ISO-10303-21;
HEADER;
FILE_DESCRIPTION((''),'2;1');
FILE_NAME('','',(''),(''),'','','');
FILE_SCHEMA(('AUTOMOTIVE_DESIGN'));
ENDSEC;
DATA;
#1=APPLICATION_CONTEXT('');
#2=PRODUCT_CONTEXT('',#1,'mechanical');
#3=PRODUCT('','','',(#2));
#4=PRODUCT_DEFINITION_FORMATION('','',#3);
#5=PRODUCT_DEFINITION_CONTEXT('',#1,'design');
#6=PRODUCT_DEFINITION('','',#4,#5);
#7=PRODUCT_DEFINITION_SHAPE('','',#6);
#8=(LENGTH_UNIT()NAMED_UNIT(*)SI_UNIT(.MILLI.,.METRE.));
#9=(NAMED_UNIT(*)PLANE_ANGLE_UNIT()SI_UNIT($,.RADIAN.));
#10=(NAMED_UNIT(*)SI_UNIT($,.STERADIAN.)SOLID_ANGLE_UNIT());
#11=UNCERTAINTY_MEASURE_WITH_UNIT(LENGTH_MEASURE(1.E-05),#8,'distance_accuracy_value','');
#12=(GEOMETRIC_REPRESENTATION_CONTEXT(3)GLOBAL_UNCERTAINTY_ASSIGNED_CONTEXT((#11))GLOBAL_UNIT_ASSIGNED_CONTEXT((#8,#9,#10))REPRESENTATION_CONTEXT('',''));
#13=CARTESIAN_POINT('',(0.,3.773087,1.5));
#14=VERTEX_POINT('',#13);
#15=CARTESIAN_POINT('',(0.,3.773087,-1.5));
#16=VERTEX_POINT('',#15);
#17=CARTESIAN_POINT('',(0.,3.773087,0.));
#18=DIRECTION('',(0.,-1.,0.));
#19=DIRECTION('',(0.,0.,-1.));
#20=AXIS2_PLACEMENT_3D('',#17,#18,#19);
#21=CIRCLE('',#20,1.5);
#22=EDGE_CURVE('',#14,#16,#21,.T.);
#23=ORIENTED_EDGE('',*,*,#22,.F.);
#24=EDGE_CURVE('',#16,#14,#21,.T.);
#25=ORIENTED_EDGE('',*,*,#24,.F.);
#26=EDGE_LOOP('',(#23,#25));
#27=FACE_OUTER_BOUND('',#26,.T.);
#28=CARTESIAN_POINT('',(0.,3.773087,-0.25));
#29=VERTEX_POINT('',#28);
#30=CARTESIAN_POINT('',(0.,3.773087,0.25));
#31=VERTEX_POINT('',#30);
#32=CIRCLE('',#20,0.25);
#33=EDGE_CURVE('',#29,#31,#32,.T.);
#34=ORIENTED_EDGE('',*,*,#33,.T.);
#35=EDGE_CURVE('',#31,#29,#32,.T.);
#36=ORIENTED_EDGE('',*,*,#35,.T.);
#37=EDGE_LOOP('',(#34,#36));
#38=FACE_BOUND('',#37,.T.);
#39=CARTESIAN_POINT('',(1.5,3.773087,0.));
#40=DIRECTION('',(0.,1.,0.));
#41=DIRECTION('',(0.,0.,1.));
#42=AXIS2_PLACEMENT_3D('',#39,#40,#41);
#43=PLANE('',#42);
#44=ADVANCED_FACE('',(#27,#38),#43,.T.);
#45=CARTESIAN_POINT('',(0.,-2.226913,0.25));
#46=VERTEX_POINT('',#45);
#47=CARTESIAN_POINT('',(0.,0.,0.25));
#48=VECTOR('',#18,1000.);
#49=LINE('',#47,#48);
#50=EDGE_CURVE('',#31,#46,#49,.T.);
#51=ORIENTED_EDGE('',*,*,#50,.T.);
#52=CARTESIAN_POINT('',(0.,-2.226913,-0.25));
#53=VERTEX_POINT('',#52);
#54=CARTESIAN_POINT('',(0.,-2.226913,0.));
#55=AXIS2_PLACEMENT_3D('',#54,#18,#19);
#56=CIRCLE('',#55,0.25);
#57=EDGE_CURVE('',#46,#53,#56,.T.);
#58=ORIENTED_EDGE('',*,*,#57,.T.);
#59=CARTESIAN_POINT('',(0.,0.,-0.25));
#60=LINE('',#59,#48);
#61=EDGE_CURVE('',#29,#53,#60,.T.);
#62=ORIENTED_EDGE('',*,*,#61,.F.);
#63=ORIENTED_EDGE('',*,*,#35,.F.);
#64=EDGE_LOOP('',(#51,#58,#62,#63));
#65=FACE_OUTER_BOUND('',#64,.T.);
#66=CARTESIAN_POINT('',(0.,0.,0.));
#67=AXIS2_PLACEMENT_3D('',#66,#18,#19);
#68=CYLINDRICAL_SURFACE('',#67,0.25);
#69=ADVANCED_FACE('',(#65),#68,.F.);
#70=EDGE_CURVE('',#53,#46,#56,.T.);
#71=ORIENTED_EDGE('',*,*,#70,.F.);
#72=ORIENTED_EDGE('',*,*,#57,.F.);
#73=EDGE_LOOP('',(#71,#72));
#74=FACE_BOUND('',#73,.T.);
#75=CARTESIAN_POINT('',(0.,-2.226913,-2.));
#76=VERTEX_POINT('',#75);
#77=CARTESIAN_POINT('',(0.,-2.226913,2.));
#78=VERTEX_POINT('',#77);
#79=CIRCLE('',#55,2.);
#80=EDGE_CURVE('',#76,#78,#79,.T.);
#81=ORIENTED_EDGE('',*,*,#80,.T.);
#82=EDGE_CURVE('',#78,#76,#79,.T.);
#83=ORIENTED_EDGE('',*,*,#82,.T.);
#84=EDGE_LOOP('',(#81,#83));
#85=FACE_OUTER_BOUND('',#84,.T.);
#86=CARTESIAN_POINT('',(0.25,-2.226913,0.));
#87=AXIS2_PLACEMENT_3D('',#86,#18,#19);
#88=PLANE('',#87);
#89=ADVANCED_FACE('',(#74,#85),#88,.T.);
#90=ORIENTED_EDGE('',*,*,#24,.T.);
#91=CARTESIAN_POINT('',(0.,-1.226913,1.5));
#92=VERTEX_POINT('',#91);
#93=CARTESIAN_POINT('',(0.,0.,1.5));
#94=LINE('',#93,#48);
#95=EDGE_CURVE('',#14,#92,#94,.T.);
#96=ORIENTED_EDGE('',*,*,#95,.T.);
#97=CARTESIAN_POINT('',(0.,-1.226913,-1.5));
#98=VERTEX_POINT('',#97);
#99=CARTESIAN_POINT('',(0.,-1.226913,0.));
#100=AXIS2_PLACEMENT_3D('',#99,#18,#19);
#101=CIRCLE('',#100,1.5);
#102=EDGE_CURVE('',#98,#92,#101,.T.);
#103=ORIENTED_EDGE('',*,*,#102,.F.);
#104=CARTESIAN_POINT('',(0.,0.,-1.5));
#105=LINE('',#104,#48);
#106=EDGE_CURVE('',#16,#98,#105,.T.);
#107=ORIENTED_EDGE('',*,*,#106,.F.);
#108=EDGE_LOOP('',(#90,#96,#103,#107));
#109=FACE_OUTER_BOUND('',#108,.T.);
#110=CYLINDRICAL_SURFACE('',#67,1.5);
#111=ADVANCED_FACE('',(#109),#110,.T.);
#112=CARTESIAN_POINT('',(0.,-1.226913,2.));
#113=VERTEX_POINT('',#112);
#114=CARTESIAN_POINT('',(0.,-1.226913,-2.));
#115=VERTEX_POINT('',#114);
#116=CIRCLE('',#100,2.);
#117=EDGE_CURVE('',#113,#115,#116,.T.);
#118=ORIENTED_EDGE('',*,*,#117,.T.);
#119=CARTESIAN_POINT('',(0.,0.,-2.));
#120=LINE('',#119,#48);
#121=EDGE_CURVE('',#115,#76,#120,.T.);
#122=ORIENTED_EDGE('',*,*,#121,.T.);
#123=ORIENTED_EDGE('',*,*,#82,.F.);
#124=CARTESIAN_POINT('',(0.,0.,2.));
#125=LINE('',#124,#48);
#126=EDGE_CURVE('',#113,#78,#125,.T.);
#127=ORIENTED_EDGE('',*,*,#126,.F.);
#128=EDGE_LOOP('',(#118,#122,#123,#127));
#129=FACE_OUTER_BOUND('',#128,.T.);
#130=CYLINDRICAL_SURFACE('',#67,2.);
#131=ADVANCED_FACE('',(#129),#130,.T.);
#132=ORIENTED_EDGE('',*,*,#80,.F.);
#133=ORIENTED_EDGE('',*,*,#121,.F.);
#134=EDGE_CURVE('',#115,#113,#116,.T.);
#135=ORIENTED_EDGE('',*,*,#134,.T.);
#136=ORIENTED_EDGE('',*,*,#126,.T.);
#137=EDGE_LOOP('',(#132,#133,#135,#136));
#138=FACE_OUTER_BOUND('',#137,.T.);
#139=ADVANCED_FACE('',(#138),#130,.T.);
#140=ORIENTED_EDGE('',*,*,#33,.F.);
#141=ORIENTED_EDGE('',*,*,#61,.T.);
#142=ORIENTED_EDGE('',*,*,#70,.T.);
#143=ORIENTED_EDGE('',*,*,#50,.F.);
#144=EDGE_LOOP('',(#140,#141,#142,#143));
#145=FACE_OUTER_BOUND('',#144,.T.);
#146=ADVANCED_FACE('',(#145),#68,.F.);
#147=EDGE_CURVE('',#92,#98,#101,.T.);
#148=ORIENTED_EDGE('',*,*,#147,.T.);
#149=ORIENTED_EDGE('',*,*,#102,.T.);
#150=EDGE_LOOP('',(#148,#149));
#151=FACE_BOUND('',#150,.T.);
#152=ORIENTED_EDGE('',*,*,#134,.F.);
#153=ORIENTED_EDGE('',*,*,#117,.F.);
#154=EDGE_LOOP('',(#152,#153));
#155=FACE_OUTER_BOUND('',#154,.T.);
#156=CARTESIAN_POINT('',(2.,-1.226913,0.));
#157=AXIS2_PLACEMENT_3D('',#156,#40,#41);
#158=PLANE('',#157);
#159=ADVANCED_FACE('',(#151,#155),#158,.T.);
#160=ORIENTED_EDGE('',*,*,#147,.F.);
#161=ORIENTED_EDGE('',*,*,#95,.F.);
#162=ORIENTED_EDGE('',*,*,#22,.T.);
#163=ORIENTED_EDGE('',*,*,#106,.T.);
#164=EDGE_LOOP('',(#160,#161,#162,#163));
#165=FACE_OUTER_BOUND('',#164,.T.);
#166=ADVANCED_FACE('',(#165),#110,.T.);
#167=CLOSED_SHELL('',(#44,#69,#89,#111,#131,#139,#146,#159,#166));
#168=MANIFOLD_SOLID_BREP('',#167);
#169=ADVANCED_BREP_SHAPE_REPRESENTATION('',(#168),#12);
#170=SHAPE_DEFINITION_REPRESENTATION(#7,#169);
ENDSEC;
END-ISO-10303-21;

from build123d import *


with BuildPart() as part:
    # 草图1 → 旋转1 (revolve)
    with BuildSketch(Plane.XY, mode=Mode.PRIVATE) as revolve_1_sk:
        Polygon((0.25, 3.773087071), (0.25, -2.226912929), (2, -2.226912929), (2, -1.226912929), (1.5, -1.226912929), (1.5, 3.773087071), align=None)
    revolve(revolve_1_sk.sketch.rotate(Axis((0, 0, 0), (0, 1, 0)), 90), axis=Axis((0, 0, 0), (0, 1, 0)))


solid = part.part
